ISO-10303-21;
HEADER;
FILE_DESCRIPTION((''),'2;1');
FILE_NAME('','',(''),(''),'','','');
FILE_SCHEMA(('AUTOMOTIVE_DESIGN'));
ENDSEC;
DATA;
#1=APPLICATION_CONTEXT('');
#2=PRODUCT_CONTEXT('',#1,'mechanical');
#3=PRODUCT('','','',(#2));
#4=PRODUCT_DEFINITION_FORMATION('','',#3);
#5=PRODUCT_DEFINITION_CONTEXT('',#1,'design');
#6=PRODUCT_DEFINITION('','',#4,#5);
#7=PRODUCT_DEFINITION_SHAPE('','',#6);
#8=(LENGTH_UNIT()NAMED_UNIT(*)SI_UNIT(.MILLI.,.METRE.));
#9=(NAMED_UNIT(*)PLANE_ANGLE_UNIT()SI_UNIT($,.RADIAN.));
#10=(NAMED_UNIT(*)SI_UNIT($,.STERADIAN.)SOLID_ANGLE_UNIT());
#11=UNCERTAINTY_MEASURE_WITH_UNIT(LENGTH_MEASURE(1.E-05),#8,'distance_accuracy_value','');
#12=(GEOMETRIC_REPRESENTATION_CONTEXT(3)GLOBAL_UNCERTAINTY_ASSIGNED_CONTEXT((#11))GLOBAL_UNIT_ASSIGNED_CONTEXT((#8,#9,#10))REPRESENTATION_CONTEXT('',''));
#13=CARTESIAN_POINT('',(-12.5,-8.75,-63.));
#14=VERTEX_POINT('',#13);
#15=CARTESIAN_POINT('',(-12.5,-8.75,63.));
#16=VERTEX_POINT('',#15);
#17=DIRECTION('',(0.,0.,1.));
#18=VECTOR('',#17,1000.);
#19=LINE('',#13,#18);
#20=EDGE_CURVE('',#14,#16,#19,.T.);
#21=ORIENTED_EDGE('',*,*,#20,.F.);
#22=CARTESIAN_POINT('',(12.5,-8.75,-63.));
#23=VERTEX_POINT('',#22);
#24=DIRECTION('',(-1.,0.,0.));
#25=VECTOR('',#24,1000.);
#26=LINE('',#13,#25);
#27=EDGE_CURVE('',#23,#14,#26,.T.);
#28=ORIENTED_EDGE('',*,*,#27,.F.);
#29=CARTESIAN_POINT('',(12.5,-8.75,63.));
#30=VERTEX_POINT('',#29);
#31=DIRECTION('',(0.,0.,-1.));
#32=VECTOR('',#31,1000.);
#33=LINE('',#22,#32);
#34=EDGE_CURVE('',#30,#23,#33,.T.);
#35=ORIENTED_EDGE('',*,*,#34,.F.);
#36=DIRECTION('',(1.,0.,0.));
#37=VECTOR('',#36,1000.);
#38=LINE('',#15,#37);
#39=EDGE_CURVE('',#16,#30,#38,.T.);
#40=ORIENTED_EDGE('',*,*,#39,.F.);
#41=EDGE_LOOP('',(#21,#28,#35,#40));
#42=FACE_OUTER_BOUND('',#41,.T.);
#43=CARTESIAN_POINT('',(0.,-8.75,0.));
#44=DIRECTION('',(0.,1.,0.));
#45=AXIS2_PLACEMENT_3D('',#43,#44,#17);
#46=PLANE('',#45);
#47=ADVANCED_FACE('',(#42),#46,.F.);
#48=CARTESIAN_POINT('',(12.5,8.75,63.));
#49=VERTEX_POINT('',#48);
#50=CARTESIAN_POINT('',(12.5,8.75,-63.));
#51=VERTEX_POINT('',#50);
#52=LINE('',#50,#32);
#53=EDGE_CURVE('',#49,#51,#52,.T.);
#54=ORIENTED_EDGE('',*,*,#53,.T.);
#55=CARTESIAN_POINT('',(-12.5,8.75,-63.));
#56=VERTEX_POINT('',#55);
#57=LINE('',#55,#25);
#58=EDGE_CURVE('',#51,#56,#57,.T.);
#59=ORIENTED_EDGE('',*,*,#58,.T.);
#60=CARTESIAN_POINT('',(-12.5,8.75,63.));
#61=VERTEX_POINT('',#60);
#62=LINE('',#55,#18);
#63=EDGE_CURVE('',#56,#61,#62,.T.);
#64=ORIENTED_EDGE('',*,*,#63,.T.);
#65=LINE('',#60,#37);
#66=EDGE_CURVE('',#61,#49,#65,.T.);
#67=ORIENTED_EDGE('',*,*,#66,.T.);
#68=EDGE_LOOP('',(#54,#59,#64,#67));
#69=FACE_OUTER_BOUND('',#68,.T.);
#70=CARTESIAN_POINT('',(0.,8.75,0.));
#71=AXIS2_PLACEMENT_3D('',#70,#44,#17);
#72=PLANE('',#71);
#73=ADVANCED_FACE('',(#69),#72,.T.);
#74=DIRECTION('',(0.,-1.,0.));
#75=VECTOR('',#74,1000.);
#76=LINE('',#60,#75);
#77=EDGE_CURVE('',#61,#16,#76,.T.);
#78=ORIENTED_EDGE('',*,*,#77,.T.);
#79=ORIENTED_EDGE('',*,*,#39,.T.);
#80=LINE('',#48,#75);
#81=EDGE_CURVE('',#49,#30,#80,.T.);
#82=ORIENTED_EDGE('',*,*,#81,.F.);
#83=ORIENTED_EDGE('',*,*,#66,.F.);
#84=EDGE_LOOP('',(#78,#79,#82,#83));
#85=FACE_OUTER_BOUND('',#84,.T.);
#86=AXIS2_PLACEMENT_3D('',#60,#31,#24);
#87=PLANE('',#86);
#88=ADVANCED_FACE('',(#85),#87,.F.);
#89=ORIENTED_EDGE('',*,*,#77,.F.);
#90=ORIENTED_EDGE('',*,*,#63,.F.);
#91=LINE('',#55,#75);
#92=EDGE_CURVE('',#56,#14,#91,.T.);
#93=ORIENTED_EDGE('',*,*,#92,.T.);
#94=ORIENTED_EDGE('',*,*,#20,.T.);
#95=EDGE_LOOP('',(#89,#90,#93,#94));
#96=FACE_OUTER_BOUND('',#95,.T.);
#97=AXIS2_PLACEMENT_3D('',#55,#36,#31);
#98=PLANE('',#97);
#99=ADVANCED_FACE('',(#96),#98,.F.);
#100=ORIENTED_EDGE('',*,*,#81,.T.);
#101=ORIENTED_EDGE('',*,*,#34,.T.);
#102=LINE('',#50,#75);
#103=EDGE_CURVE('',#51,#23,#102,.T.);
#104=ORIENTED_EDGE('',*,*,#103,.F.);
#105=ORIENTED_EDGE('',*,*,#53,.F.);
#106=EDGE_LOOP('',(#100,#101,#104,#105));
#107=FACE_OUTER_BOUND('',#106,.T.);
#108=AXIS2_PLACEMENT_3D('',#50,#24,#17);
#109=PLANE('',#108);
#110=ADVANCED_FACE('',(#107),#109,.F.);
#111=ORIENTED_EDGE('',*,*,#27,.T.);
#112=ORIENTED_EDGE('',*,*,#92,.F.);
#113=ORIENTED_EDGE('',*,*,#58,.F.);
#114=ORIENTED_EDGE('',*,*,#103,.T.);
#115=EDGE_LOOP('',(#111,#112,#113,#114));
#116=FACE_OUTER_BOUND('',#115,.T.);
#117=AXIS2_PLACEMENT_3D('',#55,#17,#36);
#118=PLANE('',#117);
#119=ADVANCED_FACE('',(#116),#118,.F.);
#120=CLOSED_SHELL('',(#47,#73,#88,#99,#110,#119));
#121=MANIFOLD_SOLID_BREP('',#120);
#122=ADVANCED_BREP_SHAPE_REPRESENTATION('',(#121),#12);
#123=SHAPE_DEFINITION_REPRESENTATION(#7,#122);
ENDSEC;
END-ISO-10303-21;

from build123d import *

# Parameters (mm, degrees)
SKETCH2_W           = 25
SKETCH2_H           = 126
BOSS_EXTRUDE1_DEPTH = 8.75


with BuildPart() as part:
    # Sketch2 → Boss-Extrude1 (new, symmetric)
    with BuildSketch(Plane(origin=(0, 0, 0), x_dir=(1, 0, 0), z_dir=(0, 1, 0))):
        Rectangle(SKETCH2_W, SKETCH2_H)
    extrude(amount=BOSS_EXTRUDE1_DEPTH, both=True)


solid = part.part
